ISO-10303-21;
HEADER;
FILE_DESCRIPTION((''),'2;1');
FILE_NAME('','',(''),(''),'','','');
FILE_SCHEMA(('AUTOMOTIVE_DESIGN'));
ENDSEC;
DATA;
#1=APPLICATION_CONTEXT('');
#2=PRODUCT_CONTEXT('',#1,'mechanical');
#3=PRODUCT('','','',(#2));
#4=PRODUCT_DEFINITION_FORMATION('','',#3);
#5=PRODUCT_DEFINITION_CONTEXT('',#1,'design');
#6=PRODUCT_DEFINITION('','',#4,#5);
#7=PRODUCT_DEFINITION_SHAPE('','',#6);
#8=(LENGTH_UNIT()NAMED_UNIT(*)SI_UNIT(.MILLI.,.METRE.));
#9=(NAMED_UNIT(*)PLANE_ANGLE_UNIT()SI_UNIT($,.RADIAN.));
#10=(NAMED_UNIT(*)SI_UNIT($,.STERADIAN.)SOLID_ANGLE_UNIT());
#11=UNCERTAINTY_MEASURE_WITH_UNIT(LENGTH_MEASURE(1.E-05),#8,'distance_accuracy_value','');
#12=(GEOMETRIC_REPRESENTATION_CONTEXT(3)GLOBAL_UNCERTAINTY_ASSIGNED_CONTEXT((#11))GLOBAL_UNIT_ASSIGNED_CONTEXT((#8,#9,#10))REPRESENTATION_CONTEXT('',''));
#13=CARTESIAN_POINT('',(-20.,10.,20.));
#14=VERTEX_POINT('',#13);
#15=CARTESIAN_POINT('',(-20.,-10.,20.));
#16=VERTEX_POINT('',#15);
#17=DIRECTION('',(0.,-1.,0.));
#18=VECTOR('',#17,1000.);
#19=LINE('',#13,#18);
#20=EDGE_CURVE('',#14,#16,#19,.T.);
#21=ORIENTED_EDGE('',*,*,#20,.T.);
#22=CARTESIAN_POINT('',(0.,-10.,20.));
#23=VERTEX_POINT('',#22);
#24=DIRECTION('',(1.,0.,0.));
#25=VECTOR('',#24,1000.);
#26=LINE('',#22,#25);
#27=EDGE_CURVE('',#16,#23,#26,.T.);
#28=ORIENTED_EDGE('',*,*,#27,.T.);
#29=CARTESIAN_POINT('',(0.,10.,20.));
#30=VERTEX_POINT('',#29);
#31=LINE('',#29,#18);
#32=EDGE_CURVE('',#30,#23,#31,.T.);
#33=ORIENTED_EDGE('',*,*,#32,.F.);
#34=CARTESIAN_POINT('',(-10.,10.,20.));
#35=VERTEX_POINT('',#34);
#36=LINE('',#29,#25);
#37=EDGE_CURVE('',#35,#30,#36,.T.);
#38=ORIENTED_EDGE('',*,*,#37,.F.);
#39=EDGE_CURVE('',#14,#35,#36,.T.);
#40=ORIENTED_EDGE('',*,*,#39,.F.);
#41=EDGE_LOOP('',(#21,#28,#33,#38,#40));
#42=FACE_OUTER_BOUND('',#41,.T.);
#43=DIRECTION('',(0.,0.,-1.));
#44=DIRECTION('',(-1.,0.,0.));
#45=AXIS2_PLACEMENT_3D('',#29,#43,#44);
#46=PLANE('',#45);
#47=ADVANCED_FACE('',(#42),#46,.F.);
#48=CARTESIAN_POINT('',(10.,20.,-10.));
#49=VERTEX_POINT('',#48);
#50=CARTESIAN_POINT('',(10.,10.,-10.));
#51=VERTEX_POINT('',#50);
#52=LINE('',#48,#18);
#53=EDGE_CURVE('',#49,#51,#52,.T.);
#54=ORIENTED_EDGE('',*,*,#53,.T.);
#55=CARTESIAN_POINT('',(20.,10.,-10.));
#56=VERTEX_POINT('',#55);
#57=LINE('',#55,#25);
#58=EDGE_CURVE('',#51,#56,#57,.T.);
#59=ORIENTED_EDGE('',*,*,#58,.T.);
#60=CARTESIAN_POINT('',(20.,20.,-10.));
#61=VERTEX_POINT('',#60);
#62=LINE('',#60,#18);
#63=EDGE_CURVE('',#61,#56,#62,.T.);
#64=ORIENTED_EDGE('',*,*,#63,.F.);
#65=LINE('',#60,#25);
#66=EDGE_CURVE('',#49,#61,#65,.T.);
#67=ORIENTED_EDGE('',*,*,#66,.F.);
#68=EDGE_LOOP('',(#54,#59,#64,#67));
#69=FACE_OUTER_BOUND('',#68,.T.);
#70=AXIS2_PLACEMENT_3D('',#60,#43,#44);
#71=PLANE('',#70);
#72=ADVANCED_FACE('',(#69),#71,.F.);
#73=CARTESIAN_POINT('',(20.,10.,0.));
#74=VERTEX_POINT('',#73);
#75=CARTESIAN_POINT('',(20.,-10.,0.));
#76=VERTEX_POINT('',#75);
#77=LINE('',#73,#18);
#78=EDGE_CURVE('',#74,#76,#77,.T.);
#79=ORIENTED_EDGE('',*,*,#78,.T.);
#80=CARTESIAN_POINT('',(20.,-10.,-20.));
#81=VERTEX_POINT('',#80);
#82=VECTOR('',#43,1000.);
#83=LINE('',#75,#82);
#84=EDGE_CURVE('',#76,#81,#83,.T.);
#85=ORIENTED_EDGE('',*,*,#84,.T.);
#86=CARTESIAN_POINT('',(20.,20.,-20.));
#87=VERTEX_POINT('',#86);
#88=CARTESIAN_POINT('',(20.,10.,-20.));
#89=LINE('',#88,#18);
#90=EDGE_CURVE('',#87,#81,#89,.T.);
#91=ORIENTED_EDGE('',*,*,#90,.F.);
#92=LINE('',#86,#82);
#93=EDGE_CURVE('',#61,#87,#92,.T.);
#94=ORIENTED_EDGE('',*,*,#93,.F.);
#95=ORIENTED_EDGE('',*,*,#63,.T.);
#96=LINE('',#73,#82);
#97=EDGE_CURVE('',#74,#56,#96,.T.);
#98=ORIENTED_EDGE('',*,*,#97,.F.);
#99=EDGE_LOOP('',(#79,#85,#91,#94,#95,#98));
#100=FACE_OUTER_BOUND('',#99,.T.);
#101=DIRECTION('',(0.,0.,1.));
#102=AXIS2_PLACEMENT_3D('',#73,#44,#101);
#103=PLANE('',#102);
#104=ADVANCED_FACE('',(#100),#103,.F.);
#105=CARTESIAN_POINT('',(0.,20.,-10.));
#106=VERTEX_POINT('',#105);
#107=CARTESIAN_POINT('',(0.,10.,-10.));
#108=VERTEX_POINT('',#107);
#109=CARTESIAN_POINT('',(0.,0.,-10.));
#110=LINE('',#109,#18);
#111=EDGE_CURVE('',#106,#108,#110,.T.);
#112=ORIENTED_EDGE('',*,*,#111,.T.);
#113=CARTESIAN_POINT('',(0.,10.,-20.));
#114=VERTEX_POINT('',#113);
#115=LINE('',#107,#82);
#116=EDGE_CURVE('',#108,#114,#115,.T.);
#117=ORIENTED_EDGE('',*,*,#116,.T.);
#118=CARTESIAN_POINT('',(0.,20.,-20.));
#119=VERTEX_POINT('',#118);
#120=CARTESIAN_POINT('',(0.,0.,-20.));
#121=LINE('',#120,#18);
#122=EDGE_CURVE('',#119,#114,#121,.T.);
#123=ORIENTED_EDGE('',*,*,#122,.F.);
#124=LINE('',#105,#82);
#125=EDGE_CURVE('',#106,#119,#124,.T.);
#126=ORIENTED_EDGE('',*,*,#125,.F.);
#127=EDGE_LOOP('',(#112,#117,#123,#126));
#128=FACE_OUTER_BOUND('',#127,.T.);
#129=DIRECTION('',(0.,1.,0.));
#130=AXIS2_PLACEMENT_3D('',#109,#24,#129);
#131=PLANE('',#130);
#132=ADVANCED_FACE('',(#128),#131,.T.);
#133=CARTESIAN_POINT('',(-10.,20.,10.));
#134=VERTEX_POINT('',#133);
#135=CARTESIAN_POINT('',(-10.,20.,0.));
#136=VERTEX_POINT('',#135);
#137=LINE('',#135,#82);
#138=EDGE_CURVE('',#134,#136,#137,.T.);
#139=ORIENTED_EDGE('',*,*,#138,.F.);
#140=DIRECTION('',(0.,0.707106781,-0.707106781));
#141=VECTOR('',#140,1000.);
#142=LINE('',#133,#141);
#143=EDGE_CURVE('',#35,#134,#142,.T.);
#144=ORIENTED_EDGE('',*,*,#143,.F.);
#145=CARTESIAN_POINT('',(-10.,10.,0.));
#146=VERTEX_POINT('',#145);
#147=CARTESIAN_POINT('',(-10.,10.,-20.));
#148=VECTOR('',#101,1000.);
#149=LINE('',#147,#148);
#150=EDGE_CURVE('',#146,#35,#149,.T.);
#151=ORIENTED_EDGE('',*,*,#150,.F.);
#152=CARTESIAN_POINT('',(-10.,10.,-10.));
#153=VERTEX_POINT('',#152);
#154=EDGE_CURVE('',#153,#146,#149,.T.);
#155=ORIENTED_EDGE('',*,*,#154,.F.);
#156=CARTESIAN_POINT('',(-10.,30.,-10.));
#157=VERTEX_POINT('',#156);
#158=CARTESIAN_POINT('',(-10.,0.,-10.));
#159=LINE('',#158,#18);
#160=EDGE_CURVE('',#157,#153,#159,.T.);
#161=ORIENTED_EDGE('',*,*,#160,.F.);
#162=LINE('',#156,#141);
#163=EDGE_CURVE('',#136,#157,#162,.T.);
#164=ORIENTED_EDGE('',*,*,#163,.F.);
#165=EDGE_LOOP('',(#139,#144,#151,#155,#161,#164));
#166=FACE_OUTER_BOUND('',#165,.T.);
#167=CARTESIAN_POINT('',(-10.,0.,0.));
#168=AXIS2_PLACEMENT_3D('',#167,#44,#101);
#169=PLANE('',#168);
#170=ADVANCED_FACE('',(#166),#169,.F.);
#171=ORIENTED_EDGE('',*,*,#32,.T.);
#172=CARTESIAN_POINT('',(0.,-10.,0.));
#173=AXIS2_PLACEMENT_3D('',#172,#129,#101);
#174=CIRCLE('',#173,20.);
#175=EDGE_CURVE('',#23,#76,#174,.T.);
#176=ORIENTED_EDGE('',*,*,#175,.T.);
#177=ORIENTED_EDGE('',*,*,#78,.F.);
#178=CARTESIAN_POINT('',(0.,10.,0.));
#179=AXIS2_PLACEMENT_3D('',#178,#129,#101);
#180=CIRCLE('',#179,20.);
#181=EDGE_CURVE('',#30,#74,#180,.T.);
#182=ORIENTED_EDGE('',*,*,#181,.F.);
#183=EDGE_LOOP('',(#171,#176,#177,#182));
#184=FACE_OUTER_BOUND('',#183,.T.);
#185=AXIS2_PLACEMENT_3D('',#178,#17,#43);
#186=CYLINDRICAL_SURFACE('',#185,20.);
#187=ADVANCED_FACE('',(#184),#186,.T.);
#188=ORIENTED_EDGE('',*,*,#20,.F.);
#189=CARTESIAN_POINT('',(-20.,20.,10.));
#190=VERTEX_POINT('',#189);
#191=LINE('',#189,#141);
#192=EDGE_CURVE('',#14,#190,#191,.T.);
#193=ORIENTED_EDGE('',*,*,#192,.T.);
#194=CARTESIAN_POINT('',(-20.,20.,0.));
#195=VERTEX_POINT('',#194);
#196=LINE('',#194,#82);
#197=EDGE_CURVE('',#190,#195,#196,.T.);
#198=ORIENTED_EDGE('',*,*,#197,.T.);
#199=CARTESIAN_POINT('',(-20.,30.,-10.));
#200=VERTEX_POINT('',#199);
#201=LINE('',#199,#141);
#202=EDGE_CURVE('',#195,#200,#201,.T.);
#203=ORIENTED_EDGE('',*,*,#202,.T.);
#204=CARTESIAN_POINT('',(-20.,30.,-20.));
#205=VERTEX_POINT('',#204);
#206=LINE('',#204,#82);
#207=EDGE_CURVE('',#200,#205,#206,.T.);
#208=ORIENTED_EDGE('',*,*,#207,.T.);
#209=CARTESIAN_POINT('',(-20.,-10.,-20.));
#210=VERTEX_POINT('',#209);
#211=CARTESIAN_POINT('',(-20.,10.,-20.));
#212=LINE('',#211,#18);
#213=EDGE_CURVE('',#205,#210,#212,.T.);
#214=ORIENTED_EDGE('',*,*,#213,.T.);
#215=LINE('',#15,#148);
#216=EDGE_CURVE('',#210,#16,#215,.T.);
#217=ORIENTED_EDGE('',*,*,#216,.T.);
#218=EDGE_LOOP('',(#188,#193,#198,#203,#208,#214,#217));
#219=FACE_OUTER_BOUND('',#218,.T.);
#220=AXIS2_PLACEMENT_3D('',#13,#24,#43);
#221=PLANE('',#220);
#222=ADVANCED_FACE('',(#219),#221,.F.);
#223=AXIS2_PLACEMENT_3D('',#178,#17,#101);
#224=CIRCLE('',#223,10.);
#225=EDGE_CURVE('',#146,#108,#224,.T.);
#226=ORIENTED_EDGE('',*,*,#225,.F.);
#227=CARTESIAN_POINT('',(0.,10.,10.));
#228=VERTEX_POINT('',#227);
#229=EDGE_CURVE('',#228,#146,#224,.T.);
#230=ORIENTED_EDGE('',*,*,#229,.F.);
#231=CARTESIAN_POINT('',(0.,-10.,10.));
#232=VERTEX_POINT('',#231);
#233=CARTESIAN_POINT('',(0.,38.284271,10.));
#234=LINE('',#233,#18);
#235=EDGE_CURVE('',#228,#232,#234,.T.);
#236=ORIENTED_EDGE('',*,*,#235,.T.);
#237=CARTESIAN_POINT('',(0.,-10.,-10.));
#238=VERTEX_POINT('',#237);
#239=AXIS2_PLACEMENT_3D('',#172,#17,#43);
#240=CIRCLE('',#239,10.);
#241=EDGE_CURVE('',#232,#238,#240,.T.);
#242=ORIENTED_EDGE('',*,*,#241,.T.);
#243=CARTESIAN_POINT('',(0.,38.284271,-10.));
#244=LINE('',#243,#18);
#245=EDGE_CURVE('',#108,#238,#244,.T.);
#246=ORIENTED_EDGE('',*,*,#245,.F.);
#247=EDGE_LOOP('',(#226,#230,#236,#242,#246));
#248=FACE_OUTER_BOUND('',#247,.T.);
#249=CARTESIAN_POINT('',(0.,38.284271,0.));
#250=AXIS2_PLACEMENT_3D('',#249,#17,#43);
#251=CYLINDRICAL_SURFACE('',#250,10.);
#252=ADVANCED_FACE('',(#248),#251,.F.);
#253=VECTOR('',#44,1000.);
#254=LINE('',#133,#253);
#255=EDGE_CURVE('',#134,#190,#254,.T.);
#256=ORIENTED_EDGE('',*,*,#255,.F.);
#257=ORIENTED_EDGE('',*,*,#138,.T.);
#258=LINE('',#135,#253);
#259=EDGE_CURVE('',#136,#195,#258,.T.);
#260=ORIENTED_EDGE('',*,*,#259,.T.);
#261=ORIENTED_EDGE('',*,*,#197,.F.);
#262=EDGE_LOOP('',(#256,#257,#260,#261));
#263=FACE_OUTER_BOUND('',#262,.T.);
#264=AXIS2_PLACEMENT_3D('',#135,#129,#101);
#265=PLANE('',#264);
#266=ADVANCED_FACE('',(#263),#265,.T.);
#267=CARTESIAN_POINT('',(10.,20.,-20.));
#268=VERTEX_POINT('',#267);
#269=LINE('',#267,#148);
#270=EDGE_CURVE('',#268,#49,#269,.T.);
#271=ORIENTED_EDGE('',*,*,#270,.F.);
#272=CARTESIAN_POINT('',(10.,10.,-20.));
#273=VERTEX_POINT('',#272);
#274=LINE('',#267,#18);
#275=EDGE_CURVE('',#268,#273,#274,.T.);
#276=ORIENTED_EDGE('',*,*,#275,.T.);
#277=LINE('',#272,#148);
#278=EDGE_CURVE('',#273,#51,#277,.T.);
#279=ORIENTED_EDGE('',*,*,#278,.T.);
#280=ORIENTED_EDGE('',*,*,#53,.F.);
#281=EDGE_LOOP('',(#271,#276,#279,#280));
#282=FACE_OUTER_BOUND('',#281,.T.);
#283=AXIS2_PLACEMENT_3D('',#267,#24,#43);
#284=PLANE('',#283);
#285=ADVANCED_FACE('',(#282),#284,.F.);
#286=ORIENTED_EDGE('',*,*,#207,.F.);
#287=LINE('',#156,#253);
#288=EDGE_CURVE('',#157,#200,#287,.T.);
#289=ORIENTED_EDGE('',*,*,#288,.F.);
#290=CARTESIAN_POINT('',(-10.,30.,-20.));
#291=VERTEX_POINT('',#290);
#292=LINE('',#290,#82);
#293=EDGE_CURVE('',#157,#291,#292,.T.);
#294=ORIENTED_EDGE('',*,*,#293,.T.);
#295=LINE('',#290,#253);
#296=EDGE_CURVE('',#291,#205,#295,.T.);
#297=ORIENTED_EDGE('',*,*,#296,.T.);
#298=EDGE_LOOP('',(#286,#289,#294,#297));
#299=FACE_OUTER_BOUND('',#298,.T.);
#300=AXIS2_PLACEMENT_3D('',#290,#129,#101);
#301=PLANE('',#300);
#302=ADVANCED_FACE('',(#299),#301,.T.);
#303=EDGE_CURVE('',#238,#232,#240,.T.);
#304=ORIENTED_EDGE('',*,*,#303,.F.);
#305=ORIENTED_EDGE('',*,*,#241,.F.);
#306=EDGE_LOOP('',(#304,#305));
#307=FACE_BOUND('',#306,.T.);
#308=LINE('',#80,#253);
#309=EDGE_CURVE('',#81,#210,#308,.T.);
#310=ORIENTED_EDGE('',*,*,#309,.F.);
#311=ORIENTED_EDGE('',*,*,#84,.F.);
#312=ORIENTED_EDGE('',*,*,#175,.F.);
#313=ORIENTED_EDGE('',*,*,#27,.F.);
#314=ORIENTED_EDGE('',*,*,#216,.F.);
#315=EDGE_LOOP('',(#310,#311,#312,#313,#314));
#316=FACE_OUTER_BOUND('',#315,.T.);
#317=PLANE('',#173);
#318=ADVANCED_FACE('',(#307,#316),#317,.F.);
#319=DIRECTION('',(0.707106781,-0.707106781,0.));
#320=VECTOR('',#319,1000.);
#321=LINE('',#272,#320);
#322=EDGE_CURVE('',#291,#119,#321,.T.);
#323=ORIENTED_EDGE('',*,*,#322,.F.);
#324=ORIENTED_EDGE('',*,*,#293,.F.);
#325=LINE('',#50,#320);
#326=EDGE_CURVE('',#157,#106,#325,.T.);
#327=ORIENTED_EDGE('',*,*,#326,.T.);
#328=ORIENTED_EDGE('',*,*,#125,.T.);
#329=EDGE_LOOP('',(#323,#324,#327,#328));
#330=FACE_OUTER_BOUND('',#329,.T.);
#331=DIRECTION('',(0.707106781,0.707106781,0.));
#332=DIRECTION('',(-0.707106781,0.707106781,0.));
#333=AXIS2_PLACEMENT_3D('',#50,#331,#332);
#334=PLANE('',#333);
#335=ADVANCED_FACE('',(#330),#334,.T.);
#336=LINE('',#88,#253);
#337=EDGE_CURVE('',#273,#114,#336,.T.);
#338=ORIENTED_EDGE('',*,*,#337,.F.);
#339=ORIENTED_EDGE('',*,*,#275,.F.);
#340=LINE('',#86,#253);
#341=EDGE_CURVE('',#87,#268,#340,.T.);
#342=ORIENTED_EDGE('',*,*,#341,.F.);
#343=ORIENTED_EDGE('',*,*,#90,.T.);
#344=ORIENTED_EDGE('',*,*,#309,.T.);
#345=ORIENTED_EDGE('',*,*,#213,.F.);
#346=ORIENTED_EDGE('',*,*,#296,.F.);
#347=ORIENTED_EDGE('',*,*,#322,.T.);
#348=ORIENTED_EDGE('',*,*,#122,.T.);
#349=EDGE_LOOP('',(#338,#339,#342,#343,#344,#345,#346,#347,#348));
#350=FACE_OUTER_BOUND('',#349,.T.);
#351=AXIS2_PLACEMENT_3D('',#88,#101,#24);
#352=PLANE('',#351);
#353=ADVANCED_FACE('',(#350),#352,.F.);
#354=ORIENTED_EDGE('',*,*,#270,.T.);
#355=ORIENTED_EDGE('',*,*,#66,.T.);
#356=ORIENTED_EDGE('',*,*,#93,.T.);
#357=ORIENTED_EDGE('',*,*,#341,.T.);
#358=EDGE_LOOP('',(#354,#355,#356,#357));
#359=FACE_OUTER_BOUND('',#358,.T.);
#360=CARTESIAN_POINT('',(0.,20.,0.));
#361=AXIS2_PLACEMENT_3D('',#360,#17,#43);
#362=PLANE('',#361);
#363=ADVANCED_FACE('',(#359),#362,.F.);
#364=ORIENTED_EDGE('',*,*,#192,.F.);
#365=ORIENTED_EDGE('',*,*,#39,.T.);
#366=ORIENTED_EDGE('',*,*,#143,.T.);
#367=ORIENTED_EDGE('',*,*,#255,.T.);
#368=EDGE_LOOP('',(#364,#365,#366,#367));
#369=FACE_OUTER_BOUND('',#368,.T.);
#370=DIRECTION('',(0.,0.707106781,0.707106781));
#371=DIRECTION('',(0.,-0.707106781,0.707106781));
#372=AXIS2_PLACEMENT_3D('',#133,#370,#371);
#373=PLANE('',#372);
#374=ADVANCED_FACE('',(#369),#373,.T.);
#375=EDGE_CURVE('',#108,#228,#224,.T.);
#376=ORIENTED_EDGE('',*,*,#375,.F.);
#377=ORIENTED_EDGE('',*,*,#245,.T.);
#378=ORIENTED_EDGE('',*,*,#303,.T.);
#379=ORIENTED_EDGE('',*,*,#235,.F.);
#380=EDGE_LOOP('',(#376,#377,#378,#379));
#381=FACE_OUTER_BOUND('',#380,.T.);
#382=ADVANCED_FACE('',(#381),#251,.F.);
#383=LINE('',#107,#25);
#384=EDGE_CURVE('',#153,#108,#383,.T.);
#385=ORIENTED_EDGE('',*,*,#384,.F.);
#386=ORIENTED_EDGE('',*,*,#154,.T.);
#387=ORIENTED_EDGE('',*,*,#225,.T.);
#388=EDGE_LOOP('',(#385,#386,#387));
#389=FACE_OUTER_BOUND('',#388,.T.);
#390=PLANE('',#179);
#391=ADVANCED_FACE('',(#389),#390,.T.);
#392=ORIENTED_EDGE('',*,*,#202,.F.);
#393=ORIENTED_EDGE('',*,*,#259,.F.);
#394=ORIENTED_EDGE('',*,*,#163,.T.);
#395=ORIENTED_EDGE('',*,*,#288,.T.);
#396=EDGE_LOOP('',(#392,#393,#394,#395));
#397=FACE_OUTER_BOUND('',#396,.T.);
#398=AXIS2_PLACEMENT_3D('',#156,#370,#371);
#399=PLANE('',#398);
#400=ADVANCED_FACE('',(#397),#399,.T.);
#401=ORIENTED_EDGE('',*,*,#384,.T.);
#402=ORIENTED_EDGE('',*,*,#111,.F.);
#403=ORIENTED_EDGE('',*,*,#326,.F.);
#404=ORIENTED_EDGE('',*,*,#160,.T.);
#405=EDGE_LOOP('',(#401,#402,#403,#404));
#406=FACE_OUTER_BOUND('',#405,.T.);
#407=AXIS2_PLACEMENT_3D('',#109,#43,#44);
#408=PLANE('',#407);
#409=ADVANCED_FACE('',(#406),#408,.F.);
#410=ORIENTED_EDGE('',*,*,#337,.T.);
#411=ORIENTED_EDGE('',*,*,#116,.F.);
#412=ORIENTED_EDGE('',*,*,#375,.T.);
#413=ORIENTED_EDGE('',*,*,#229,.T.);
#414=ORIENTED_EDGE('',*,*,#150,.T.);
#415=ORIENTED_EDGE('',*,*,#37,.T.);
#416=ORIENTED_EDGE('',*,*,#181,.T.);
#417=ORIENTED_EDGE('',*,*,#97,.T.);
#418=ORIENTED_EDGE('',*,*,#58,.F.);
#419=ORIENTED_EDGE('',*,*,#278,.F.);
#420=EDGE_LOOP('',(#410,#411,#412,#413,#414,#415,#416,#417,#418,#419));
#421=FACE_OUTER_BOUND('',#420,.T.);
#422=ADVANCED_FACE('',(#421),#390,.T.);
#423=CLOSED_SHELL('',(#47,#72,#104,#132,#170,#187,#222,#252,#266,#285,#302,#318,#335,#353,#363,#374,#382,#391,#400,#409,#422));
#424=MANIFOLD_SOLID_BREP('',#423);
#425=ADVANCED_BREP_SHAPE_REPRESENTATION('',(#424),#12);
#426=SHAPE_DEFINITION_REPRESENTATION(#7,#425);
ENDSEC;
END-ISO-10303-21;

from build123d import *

# Parameters (mm, degrees)
BASE_BLOCK_DEPTH        = 10
CORNER_POST_PROFILE_W   = 10
CORNER_POST_PROFILE_H   = 10
CORNER_POST_10X10_DEPTH = 10
STEPPED_RIB_DEPTH       = 10
GUSSET_DEPTH            = 10
BORE_PROFILE_R          = 10
BORE_20_DEPTH           = 20


with BuildPart() as part:
    # Base Block Profile → Base Block (new, symmetric)
    with BuildSketch(Plane(origin=(0, 0, 0), x_dir=(1, 0, 0), z_dir=(0, 1, 0))):
        with BuildLine():
            Line((0, -20), (-20, -20))
            Line((-20, -20), (-20, 20))
            Line((-20, 20), (20, 20))
            Line((20, 20), (20, 0))
            ThreePointArc((20, 0), (14.142135624, -14.142135624), (0, -20))
        make_face()
    extrude(amount=BASE_BLOCK_DEPTH, both=True)

    # Corner Post Profile → Corner Post 10x10 (add)
    with BuildSketch(Plane(origin=(0, 10, 0), x_dir=(1, 0, 0), z_dir=(0, 1, 0))):
        with Locations((15, 15)):
            Rectangle(CORNER_POST_PROFILE_W, CORNER_POST_PROFILE_H)
    extrude(amount=CORNER_POST_10X10_DEPTH)

    # Stepped Rib Profile → Stepped Rib (add)
    with BuildSketch(Plane.ZY.offset(20)):
        Polygon((-20, 10), (-20, 30), (-10, 30), (0, 20), (10, 20), (20, 10), align=None)
    extrude(amount=-STEPPED_RIB_DEPTH)

    # Gusset Profile → Gusset (add)
    with BuildSketch(Plane(origin=(0, 0, -20), x_dir=(-1, 0, 0), z_dir=(0, 0, -1))):
        Polygon((10, 10), (10, 30), (0, 20), (0, 10), align=None)
    extrude(amount=-GUSSET_DEPTH)

    # Bore Profile → Bore Ø20 (cut)
    with BuildSketch(Plane.XZ.offset(10)):
        with Locations(Location((0, 0, 0), (0, 0, 270))):
            Circle(BORE_PROFILE_R)
    extrude(amount=-BORE_20_DEPTH, mode=Mode.SUBTRACT)


solid = part.part
